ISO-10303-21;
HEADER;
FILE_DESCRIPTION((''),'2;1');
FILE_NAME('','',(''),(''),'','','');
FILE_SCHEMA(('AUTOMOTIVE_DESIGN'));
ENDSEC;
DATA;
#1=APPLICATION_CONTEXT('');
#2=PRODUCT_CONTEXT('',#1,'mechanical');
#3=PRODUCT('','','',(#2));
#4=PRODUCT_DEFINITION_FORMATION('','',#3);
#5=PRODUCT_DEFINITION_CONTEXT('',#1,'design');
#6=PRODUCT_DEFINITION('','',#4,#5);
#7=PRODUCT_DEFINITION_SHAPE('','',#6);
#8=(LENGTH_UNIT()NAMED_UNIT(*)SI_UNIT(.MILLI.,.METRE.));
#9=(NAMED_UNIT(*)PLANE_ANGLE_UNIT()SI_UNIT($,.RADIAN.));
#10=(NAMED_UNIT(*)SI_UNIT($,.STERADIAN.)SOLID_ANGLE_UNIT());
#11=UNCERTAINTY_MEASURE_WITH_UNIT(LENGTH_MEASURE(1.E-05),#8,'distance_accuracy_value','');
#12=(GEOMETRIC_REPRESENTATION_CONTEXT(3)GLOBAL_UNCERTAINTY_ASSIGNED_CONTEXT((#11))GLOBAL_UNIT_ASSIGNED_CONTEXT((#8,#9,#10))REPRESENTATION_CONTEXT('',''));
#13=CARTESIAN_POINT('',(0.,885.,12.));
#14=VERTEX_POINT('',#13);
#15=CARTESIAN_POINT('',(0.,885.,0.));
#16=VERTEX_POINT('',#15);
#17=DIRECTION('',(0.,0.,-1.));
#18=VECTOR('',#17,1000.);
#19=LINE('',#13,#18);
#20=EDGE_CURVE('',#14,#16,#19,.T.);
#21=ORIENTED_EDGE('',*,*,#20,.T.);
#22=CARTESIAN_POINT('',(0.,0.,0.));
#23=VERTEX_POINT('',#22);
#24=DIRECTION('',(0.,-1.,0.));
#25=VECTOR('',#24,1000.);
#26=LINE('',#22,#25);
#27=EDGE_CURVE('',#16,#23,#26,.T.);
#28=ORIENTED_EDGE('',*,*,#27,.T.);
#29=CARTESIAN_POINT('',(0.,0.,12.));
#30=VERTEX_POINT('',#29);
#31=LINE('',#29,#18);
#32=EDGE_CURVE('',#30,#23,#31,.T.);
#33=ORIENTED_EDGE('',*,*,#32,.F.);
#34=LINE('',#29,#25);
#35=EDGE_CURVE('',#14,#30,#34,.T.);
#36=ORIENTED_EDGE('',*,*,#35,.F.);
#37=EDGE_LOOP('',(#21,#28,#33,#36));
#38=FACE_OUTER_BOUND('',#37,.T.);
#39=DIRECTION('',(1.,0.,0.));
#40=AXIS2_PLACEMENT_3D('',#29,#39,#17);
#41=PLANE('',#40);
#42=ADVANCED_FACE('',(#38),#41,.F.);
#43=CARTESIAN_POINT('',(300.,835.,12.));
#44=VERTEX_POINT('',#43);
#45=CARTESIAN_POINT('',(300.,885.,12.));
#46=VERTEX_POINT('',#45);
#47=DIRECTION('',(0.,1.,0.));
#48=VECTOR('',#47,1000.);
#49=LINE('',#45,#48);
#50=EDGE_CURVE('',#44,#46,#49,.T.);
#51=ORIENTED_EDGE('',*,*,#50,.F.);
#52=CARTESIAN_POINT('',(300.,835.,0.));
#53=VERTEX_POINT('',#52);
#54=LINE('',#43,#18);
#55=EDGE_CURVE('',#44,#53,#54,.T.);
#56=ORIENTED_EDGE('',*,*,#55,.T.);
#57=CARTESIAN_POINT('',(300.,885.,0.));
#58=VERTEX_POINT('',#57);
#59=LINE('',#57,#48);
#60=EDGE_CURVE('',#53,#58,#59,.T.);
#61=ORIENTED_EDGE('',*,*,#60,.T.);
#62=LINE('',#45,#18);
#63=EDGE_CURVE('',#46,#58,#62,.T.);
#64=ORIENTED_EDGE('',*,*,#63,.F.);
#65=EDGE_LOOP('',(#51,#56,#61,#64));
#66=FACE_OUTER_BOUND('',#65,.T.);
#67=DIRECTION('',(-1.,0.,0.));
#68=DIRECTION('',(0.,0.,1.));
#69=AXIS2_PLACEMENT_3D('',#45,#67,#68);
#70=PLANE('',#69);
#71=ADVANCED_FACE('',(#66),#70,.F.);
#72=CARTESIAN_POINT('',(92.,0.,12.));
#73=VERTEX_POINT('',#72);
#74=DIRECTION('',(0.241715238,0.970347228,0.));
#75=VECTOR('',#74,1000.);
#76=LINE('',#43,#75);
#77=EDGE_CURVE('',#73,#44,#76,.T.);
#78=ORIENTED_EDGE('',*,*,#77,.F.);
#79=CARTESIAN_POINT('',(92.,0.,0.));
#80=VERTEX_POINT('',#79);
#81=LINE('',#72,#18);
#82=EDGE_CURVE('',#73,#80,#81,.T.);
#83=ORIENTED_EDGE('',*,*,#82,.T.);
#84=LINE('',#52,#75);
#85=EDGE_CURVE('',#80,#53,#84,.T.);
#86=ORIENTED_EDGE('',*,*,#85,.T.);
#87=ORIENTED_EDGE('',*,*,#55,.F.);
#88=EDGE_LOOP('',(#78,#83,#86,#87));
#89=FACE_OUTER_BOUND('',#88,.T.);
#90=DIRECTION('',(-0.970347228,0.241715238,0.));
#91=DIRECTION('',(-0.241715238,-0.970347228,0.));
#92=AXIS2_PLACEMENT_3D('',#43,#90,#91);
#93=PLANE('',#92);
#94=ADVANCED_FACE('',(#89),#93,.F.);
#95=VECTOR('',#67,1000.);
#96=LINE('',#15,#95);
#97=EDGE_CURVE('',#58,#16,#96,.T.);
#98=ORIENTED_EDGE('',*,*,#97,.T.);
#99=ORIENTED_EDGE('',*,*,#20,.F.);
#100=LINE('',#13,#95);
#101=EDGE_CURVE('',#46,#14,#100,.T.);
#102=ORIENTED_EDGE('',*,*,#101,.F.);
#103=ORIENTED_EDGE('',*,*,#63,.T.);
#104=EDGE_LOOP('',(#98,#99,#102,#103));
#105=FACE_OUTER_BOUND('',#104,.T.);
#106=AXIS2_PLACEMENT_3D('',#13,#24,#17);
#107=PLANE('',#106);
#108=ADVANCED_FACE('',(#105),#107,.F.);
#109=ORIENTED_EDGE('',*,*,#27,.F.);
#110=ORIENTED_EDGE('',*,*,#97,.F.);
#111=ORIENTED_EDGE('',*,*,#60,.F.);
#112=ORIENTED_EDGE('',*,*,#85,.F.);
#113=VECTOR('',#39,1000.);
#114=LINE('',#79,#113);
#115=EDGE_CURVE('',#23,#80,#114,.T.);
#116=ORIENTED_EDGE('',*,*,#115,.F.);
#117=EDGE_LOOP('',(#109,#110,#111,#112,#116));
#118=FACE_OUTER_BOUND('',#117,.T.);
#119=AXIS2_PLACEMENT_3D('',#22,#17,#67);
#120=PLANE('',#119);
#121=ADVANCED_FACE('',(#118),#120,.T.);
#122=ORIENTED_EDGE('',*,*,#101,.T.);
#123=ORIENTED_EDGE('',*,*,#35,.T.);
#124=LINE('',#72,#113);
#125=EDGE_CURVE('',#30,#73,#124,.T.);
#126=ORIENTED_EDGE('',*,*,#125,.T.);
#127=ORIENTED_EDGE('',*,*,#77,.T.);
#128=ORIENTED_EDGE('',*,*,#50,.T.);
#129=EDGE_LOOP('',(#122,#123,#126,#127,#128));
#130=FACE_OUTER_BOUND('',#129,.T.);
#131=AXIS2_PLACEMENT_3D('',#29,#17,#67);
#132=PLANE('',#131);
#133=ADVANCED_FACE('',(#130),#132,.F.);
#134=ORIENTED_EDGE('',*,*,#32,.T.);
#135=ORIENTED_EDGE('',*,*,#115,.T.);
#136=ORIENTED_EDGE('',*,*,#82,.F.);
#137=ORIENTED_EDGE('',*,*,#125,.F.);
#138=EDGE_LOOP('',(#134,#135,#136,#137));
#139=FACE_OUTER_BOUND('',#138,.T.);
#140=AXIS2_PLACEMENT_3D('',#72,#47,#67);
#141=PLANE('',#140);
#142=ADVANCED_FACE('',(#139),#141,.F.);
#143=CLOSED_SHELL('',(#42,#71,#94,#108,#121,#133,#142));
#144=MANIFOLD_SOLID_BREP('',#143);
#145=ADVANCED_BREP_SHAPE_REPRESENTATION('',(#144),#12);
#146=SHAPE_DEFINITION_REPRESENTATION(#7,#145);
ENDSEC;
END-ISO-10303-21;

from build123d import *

# Parameters (mm, degrees)
BOSS_EXTRUDE1_DEPTH = 12


with BuildPart() as part:
    # Sketch1 → Boss-Extrude1 (new body)
    with BuildSketch(Plane.XY):
        Polygon((0, 0), (0, 885), (300, 885), (300, 835), (92, 0), align=None)
    extrude(amount=BOSS_EXTRUDE1_DEPTH)


solid = part.part
